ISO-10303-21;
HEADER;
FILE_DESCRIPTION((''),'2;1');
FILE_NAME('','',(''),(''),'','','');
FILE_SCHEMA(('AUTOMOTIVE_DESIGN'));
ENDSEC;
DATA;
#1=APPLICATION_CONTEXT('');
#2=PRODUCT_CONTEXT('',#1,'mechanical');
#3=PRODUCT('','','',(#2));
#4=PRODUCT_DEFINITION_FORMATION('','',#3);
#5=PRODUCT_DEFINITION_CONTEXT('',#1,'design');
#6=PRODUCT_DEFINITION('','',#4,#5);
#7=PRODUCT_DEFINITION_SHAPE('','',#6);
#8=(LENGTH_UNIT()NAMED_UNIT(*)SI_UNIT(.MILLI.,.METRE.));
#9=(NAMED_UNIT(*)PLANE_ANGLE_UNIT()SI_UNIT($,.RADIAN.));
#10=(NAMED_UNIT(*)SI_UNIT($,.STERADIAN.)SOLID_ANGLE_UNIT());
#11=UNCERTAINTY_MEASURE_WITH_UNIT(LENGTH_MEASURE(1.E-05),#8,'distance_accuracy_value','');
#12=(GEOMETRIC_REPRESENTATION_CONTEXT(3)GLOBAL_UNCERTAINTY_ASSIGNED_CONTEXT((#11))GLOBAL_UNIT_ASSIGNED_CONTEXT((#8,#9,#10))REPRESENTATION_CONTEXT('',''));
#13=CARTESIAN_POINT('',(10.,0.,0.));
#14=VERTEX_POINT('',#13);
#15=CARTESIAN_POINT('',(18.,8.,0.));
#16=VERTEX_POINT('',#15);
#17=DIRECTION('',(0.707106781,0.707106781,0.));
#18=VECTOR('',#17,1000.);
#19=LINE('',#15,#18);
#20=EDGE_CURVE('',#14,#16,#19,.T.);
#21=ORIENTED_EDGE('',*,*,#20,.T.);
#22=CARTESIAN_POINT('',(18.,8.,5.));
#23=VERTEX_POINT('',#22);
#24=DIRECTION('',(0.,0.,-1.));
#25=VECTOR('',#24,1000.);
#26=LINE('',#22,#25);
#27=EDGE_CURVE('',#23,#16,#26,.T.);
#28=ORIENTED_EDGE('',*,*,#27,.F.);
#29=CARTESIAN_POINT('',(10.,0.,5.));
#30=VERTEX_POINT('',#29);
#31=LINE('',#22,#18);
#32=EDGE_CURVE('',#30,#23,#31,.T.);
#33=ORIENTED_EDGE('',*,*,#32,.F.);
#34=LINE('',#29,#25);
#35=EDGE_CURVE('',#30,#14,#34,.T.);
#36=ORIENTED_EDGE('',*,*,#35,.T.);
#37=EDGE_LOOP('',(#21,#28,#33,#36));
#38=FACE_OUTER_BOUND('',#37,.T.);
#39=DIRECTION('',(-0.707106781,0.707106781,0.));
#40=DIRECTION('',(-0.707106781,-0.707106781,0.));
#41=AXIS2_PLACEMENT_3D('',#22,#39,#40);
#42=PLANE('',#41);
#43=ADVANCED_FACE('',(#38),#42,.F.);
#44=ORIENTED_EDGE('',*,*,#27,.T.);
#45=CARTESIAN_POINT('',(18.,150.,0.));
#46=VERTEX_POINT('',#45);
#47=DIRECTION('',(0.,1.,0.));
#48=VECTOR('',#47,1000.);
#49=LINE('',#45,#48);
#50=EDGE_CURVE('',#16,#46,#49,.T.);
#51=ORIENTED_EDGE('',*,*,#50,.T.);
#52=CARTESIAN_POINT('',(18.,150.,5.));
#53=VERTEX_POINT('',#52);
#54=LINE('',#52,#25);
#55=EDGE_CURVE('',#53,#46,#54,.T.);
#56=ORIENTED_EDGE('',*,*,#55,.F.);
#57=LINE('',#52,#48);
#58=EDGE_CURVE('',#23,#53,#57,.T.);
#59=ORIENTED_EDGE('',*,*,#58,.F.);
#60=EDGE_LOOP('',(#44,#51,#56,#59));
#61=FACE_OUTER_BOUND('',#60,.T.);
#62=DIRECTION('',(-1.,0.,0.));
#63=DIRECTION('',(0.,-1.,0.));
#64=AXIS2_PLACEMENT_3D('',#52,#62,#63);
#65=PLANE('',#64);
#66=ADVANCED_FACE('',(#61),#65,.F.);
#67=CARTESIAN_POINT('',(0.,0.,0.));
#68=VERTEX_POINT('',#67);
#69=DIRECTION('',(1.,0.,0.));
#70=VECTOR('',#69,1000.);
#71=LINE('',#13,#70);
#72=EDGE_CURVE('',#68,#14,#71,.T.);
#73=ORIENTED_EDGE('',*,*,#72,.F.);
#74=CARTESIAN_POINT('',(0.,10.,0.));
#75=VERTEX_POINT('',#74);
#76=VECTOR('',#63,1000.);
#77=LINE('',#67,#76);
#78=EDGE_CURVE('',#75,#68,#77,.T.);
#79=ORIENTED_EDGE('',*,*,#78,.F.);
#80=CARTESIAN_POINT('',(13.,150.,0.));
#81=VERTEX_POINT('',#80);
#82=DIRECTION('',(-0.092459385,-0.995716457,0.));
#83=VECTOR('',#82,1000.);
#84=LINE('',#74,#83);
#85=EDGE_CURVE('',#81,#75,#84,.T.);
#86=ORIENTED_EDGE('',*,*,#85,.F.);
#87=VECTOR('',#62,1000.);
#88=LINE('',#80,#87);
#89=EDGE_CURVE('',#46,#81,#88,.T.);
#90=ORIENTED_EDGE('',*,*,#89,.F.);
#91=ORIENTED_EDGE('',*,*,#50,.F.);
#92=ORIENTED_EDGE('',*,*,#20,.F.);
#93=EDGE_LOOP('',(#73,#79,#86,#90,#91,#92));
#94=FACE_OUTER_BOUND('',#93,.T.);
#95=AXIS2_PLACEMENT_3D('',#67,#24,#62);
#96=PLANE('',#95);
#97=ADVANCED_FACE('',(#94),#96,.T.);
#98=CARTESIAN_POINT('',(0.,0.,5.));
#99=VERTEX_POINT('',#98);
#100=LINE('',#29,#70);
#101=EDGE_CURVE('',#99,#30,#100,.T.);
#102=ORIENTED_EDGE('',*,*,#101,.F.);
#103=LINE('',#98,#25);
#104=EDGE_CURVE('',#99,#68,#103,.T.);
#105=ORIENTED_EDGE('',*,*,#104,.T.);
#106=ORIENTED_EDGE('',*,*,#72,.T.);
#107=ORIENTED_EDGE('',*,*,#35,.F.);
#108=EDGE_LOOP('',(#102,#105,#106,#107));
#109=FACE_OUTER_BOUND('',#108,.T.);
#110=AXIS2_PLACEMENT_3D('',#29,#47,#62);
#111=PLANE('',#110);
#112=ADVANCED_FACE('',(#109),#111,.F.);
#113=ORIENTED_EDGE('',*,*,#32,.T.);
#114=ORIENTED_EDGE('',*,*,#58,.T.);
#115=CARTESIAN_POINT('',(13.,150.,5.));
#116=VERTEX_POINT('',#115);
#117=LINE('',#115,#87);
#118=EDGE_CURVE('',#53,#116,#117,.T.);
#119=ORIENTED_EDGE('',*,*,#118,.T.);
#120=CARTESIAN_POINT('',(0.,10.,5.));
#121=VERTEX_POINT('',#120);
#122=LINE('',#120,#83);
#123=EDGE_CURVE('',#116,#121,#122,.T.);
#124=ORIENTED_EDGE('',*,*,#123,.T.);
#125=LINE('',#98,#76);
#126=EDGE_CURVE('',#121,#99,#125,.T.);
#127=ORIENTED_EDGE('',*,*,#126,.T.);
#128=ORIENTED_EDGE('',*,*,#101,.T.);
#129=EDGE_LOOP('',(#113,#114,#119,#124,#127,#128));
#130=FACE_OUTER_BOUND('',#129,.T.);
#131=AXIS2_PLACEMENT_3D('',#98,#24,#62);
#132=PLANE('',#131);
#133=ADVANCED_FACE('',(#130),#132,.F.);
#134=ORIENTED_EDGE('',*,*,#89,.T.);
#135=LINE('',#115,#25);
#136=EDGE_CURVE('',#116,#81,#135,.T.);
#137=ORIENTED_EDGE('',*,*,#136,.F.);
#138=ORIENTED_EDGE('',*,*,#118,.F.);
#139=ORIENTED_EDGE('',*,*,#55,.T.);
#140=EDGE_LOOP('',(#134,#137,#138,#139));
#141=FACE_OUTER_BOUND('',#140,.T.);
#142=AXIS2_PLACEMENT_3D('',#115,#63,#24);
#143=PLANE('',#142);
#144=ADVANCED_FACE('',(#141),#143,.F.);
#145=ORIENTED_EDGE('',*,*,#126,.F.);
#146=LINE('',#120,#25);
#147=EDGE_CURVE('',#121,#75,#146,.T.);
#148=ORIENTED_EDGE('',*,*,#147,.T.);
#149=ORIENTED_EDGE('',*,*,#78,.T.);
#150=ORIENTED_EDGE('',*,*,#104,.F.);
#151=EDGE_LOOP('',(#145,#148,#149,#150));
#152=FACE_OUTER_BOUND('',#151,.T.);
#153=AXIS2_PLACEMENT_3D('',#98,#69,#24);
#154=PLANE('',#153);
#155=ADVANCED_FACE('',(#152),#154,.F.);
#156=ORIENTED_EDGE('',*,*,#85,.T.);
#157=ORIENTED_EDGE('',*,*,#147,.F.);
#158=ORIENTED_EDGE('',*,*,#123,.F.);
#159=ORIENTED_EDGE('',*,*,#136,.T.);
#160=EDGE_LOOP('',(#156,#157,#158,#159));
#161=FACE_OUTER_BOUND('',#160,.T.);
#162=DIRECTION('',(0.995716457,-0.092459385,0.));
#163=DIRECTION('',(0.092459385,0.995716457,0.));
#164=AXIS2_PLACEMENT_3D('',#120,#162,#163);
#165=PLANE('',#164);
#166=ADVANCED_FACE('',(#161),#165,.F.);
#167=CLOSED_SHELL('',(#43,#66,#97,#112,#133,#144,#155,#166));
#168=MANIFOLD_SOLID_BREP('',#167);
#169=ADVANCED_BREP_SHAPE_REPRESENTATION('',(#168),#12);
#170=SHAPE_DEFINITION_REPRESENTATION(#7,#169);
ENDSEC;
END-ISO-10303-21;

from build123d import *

# Parameters (mm, degrees)
BOSS_EXTRUDE1_DEPTH = 5


with BuildPart() as part:
    # Sketch1 → Boss-Extrude1 (new body)
    with BuildSketch(Plane.XY):
        Polygon((0, 0), (0, 10), (13, 150), (18, 150), (18, 8), (10, 0), align=None)
    extrude(amount=BOSS_EXTRUDE1_DEPTH)


solid = part.part
